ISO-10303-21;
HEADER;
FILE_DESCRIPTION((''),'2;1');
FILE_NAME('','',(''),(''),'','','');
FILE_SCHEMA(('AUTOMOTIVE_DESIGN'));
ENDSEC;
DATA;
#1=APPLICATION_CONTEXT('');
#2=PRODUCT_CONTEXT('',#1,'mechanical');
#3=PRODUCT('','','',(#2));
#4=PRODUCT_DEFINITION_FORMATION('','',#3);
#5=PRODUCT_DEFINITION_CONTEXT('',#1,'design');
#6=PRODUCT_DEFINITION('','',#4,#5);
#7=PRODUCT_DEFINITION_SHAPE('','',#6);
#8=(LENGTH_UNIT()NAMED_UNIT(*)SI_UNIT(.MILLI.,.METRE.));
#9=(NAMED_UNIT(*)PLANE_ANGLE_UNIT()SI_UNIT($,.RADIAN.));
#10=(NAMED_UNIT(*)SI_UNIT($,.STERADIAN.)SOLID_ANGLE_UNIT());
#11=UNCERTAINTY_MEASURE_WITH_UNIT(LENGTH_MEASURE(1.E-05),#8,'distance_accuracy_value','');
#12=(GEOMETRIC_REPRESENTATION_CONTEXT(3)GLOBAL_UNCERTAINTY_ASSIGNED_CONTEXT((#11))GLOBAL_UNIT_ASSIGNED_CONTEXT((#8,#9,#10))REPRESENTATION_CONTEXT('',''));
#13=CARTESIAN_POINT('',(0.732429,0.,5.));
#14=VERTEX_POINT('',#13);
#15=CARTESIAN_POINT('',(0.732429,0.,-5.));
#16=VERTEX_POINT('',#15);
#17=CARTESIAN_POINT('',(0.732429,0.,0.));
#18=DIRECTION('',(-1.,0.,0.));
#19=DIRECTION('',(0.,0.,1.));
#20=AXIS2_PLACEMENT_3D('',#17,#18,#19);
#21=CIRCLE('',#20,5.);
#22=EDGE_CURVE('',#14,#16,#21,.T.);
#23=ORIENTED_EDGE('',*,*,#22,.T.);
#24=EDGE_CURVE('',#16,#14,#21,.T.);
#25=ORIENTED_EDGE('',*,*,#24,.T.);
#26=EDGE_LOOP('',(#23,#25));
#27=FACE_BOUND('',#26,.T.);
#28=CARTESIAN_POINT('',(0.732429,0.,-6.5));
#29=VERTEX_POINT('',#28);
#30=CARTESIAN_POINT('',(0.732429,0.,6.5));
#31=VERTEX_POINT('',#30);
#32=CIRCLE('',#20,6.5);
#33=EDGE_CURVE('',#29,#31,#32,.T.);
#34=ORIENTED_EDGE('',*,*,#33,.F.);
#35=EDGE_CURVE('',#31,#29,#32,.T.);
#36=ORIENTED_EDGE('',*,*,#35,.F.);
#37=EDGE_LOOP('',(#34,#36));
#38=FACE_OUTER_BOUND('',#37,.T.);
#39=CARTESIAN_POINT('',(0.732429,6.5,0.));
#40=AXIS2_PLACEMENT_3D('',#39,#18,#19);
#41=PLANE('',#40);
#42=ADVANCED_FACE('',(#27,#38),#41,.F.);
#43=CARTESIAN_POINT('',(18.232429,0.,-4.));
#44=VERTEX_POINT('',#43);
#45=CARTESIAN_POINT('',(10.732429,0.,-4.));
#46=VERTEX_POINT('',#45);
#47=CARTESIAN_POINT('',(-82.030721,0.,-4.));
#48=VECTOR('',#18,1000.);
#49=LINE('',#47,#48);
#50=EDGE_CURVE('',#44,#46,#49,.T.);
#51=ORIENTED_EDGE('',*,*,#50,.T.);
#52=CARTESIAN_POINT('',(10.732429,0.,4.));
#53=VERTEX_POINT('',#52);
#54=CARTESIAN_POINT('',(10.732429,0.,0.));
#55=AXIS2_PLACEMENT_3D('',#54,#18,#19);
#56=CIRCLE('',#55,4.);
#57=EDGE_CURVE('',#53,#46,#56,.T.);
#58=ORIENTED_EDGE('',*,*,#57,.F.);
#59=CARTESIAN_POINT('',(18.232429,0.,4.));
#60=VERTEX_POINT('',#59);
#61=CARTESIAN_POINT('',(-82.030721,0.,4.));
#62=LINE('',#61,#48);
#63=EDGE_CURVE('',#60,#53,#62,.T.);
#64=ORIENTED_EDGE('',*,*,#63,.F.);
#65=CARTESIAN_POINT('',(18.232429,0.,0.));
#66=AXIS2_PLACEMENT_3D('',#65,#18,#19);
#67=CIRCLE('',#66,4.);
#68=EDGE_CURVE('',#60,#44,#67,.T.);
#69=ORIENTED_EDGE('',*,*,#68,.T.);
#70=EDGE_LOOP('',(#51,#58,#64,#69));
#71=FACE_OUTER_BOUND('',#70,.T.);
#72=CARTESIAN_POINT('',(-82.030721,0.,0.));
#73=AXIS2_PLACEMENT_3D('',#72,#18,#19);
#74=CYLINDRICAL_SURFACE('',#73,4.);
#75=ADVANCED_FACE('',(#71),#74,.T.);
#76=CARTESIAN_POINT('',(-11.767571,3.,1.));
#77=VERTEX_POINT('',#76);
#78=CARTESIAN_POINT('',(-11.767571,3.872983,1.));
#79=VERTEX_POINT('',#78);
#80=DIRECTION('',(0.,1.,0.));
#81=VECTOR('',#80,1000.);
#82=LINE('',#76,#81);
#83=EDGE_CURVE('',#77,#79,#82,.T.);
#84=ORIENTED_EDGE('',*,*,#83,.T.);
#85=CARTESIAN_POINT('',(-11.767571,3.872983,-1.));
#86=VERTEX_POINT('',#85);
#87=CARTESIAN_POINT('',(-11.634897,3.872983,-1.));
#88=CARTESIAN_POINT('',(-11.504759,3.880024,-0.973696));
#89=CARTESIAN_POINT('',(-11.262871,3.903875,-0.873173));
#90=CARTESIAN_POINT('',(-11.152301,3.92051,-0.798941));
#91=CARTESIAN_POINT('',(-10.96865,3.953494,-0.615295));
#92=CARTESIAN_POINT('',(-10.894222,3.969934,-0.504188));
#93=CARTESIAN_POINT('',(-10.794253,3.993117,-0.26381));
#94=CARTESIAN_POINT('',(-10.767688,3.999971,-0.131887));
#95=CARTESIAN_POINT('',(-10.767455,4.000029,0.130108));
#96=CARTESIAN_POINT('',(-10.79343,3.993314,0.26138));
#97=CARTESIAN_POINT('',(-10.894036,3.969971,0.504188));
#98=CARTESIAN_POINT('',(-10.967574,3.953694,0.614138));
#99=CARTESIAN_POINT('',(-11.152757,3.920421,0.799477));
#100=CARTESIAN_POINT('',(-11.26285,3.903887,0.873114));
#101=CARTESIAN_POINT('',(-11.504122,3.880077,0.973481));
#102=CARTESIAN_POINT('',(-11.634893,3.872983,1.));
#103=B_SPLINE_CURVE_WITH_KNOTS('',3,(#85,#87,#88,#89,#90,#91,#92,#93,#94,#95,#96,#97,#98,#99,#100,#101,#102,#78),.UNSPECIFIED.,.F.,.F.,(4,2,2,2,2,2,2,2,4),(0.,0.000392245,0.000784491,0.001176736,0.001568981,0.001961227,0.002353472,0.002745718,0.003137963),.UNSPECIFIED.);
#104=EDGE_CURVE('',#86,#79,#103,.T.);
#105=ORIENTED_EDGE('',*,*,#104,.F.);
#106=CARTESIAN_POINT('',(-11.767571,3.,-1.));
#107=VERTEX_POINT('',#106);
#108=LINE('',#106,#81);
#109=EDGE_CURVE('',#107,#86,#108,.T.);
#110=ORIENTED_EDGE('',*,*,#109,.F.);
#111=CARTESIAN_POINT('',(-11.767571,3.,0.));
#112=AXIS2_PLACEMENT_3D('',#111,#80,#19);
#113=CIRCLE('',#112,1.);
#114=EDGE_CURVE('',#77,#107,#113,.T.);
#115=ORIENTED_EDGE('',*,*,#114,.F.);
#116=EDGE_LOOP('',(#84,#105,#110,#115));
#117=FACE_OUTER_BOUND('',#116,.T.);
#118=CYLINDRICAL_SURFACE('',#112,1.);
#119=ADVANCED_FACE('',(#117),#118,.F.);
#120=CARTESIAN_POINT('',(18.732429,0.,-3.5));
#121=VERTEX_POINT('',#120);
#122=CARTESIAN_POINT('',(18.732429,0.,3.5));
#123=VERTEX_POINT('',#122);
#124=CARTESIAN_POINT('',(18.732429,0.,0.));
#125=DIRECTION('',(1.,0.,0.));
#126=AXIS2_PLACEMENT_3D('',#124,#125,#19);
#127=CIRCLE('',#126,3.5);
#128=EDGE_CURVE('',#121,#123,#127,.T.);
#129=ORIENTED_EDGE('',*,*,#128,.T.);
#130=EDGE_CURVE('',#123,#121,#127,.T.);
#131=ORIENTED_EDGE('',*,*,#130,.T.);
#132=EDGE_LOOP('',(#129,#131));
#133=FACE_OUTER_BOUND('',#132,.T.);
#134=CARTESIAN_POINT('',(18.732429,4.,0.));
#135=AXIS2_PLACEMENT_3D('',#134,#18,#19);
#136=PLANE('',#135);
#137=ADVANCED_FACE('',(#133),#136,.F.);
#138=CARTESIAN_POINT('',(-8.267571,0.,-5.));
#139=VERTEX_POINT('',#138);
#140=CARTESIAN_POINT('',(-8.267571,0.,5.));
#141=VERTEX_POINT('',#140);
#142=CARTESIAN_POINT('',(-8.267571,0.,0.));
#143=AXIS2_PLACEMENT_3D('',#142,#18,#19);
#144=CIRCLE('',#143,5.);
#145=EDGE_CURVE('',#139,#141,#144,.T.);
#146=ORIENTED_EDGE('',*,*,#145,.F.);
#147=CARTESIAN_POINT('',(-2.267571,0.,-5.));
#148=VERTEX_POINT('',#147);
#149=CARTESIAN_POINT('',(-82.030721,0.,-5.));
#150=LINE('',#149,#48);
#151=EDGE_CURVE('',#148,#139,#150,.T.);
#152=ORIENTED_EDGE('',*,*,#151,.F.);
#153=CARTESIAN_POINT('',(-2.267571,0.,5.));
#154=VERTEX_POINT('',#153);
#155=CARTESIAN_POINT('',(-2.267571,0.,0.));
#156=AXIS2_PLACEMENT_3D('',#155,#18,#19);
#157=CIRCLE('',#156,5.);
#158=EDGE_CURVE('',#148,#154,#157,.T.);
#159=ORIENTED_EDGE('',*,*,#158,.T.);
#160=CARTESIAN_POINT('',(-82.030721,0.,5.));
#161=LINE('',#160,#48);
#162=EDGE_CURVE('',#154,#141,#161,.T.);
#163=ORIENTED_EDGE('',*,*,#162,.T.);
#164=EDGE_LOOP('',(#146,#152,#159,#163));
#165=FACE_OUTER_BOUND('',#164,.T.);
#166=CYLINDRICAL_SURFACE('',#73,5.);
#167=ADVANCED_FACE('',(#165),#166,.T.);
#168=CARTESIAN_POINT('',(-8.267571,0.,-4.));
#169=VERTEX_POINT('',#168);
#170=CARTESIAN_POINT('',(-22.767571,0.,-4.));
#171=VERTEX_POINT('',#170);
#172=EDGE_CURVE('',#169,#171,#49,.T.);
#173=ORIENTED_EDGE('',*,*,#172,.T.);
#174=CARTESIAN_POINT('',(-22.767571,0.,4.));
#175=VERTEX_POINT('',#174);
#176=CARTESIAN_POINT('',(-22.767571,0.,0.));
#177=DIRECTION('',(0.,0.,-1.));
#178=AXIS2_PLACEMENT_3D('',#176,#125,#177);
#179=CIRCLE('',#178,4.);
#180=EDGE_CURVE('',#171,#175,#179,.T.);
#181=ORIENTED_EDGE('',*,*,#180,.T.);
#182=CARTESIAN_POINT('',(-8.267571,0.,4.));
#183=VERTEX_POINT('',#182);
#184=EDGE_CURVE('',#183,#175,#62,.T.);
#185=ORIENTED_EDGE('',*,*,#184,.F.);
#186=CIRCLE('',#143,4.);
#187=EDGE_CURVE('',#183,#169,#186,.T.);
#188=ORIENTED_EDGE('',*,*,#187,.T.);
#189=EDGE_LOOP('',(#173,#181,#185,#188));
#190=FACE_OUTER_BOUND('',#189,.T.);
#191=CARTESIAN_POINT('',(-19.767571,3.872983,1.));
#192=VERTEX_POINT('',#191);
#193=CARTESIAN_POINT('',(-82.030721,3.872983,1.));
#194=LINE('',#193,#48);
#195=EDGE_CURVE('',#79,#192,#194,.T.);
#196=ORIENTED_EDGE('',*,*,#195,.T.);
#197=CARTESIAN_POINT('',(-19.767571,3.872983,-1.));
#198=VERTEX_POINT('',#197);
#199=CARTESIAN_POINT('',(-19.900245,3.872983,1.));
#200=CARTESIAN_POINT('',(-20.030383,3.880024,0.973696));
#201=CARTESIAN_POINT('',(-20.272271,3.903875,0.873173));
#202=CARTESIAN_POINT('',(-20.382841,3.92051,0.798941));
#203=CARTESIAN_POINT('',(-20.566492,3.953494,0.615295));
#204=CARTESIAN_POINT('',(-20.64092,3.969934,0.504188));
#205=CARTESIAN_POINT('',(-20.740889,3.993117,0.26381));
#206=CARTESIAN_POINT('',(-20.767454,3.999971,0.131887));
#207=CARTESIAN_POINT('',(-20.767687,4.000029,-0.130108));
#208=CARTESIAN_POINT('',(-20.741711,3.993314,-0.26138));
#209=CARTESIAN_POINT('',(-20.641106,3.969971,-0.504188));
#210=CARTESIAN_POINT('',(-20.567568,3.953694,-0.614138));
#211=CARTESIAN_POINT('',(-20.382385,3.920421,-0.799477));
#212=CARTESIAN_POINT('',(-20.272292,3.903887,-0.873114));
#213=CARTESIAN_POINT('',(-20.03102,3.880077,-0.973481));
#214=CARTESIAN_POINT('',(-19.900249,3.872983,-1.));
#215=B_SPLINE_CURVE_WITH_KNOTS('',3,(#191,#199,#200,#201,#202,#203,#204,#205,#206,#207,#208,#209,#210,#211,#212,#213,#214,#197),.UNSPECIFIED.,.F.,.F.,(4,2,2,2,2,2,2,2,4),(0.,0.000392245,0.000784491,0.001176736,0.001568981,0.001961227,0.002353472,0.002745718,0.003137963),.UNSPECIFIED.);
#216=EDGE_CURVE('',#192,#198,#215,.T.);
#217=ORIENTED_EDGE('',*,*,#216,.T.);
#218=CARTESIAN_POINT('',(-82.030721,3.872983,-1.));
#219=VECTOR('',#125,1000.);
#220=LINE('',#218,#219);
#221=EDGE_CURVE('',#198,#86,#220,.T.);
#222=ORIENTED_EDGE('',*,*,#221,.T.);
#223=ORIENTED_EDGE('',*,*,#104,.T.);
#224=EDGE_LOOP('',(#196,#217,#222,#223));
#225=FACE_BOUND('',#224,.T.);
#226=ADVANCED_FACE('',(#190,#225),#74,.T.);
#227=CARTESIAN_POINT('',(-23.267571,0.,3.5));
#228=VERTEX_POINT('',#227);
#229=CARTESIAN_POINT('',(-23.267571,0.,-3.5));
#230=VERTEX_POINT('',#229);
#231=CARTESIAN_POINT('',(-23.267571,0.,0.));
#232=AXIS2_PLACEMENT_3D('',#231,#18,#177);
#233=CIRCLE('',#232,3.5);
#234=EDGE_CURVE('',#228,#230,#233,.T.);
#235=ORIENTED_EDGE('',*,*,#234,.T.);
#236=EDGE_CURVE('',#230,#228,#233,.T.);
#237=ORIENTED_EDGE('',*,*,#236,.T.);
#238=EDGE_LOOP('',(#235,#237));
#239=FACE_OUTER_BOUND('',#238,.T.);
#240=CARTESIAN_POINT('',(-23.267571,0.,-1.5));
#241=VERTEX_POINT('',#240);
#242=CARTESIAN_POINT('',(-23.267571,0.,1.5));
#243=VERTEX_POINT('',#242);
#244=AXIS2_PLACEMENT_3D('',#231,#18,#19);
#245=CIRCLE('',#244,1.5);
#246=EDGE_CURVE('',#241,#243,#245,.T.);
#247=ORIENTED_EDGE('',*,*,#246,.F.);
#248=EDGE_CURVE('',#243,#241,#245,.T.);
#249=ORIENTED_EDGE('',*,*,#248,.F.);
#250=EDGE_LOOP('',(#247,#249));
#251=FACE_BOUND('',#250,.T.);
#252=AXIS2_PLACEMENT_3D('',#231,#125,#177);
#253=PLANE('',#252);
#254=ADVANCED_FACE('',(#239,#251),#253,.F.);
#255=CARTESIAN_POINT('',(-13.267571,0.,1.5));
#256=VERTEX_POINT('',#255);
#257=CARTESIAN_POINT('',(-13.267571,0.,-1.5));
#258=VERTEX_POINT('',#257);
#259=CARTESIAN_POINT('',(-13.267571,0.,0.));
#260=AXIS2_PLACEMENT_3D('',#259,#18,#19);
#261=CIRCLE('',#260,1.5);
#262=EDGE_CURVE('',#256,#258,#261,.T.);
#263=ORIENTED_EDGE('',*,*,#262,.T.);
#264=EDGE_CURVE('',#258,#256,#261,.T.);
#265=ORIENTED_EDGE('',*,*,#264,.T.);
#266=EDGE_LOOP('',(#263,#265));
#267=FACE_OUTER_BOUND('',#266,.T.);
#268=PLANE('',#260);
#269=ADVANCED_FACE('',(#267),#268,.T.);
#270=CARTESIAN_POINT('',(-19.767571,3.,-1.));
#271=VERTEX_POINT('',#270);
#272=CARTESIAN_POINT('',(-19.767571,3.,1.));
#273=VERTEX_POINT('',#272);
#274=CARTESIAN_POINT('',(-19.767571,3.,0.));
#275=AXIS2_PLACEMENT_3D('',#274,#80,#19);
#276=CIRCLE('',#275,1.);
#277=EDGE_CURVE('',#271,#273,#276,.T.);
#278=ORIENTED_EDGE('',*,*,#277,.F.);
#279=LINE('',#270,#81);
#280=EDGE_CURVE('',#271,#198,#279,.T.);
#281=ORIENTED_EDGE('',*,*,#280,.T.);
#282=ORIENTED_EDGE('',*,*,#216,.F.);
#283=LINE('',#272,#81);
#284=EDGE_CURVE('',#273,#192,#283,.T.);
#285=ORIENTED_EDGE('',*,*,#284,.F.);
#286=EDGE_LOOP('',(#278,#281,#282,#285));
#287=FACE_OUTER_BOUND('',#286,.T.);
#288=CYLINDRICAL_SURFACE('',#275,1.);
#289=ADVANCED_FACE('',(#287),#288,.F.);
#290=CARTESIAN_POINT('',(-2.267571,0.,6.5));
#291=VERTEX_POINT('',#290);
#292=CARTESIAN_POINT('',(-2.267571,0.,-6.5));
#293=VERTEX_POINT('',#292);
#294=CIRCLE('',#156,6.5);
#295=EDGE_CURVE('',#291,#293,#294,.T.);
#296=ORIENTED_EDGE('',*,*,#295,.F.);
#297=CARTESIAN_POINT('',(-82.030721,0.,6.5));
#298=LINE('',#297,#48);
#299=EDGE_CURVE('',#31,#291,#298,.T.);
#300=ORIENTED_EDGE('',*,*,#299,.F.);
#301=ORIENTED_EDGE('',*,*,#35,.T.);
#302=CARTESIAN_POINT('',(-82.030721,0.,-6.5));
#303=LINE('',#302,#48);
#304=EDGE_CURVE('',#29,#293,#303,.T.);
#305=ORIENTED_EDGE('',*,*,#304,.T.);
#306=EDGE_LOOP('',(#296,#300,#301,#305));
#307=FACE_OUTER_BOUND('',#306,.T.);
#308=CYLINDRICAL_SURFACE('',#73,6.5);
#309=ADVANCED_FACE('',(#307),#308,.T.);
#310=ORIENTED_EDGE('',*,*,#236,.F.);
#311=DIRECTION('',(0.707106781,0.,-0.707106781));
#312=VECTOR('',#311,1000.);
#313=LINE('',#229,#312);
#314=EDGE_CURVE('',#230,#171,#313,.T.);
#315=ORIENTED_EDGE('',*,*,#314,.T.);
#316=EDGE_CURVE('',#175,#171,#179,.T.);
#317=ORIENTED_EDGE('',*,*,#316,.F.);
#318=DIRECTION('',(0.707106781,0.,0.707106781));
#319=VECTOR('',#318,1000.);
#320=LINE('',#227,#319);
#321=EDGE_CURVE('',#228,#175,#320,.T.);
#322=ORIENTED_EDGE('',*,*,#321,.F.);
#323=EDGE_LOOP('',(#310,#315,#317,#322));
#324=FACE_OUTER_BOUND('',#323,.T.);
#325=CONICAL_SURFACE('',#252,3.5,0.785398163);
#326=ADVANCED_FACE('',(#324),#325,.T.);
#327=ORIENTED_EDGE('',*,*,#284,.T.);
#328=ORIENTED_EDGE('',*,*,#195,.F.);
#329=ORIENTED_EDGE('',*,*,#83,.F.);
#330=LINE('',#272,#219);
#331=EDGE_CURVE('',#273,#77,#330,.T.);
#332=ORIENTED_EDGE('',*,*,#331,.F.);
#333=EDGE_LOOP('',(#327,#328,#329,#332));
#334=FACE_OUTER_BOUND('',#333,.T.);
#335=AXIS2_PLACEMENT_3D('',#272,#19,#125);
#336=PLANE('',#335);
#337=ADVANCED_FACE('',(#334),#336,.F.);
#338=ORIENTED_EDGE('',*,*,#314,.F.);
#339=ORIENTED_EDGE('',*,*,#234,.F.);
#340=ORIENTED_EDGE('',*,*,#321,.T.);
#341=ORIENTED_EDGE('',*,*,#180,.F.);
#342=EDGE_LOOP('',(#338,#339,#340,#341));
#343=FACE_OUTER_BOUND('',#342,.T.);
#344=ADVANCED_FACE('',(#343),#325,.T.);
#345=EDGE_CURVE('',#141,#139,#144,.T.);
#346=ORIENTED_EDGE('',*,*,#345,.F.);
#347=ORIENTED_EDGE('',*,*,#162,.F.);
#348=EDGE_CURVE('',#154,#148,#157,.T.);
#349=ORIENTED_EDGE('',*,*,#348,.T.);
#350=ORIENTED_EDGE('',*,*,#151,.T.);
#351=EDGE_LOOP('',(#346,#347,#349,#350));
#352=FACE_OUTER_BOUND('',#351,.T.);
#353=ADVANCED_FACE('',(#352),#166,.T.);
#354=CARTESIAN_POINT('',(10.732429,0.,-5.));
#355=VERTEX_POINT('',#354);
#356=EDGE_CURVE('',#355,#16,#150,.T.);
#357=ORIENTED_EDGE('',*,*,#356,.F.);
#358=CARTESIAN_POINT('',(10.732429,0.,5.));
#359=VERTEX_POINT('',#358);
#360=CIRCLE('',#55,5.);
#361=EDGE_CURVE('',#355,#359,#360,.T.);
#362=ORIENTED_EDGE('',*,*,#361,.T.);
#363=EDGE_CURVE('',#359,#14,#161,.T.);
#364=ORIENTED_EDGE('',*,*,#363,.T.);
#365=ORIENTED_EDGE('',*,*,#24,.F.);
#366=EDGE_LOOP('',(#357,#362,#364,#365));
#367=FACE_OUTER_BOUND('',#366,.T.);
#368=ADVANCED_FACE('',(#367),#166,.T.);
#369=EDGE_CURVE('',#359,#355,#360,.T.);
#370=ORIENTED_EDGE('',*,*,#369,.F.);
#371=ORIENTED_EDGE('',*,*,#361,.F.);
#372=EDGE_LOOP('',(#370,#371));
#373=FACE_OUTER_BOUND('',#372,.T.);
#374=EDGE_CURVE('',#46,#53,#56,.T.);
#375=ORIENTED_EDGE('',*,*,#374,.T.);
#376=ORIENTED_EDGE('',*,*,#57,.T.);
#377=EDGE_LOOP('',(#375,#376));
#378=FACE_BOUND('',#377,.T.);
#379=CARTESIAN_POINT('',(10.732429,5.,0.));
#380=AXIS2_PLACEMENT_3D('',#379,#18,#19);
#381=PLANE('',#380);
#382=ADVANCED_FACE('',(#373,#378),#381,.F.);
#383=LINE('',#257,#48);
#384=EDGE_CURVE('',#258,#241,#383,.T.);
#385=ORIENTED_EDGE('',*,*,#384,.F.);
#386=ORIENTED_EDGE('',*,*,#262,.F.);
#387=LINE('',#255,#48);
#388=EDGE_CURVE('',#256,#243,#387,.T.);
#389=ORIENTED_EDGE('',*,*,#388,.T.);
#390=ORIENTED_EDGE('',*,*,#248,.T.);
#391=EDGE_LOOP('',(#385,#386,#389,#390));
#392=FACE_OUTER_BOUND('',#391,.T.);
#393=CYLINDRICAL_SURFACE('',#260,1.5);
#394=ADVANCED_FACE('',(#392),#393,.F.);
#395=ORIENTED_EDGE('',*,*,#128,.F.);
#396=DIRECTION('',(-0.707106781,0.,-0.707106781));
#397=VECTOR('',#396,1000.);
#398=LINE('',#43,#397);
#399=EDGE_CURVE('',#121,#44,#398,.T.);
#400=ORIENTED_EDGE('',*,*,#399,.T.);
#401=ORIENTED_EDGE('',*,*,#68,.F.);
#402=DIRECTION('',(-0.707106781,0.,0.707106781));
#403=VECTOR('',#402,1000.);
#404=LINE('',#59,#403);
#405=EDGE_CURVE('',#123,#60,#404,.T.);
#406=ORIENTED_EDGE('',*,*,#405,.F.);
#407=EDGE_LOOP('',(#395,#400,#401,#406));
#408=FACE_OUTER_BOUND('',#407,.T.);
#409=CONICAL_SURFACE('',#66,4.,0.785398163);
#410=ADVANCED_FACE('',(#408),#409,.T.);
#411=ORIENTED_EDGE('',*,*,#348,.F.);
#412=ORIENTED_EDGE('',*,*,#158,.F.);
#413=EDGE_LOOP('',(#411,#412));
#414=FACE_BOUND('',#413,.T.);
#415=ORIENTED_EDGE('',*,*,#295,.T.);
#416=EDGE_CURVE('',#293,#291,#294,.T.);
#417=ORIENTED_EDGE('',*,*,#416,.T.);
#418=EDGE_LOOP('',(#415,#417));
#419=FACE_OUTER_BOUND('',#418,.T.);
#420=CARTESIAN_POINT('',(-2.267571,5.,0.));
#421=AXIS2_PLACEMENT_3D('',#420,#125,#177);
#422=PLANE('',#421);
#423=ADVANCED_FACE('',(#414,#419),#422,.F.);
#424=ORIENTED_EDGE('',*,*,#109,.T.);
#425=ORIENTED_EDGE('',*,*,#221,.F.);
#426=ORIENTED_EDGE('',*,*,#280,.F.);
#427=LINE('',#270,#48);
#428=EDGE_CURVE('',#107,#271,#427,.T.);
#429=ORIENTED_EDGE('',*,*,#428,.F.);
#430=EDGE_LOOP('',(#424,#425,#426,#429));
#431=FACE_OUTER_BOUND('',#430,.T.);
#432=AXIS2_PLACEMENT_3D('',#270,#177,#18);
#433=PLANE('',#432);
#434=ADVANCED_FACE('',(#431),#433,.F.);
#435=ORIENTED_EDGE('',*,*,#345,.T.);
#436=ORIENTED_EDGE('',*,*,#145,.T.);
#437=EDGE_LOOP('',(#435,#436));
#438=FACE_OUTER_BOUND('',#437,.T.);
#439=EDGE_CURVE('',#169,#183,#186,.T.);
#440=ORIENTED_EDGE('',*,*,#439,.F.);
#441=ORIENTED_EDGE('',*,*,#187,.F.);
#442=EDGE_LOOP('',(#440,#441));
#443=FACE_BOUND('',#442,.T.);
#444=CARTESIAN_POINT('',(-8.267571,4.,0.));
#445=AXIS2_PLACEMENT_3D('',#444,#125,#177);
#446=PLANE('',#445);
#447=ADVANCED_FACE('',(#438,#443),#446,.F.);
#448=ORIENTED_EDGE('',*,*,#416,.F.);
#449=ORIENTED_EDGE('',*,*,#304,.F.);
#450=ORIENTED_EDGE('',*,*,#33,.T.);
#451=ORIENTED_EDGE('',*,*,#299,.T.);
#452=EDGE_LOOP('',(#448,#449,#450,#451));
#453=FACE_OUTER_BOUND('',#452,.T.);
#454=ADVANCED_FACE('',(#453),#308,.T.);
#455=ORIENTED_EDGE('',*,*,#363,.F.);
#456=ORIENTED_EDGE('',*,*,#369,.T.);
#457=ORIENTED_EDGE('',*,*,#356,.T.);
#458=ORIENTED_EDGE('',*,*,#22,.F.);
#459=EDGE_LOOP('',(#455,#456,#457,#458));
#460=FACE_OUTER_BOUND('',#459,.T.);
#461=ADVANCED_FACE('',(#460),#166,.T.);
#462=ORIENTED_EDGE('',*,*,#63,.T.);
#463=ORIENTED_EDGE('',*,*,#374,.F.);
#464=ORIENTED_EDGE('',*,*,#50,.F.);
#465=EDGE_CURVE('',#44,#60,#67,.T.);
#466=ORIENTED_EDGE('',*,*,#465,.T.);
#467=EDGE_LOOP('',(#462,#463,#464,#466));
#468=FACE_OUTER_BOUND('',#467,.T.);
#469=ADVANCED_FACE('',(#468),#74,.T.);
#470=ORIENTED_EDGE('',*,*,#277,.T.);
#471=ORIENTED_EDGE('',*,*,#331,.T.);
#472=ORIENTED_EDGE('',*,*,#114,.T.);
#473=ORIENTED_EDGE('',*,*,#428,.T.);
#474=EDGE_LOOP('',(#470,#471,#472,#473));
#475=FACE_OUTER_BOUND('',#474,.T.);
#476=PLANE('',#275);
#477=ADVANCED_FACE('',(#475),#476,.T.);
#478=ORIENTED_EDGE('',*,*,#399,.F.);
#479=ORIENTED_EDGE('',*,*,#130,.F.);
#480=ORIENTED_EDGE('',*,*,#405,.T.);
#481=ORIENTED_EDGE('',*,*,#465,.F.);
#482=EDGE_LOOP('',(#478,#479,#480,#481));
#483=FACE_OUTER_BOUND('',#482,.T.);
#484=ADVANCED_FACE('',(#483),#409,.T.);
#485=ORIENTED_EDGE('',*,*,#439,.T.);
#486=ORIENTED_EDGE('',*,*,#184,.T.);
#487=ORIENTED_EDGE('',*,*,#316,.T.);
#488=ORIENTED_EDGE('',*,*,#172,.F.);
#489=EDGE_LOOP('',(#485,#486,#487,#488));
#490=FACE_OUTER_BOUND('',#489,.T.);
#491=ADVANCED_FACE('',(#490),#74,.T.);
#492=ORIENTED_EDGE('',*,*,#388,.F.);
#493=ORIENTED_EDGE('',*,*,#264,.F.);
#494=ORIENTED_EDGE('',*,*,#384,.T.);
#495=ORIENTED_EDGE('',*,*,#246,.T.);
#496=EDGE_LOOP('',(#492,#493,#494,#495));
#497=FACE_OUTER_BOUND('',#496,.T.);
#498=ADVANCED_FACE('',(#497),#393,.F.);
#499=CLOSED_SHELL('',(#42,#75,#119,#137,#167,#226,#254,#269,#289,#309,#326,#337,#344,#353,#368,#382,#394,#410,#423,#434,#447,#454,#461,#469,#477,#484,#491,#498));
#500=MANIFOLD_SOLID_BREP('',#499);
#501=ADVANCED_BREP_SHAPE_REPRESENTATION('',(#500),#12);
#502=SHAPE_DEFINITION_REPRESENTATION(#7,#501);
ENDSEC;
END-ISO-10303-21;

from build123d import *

# Parameters (mm, degrees)
CUT_EXTRUDE_3_DEPTH = 1
SKETCH_5_R          = 1.5
CUT_EXTRUDE_4_DEPTH = 10
CHAMFER_1_SIZE      = 0.5
CHAMFER_2_SIZE      = 0.5


with BuildPart() as part:
    # 草图1 → 旋转2 (revolve)
    with BuildSketch(Plane.XY, mode=Mode.PRIVATE) as revolve_2_sk:
        Polygon((-23.267570956, 0), (-23.267570956, 4), (-8.267570956, 4), (-8.267570956, 5), (-2.267570956, 5), (-2.267570956, 6.5), (0.732429044, 6.5), (0.732429044, 5), (10.732429044, 5), (10.732429044, 4), (18.732429044, 4), (18.732429044, 0), align=None)
    revolve(revolve_2_sk.sketch.rotate(Axis((-82.03072058, 0, 0), (1, 0, 0)), 90), axis=Axis((-82.03072058, 0, 0), (1, 0, 0)))

    # 草图4 → 切除-拉伸3 (cut)
    with BuildSketch(Plane(origin=(0, 4, 0), x_dir=(1, 0, 0), z_dir=(0, 1, 0))):
        with BuildLine():
            Line((-19.767570956, 1), (-11.767570956, 1))
            ThreePointArc((-11.767570956, 1), (-10.767570956, 0), (-11.767570956, -1))
            Line((-11.767570956, -1), (-19.767570956, -1))
            ThreePointArc((-19.767570956, -1), (-20.767570956, 0), (-19.767570956, 1))
        make_face()
    extrude(amount=-CUT_EXTRUDE_3_DEPTH, mode=Mode.SUBTRACT)

    # 草图5 → 切除-拉伸4 (cut)
    with BuildSketch(Plane.ZY.offset(23.267570956)):
        Circle(SKETCH_5_R)
    extrude(amount=-CUT_EXTRUDE_4_DEPTH, mode=Mode.SUBTRACT)

    # 倒角1
    chamfer_1_edges = [part.edges().sort_by_distance(p)[0] for p in [
        (-23.267570956, 0, -4),
    ]]
    chamfer(chamfer_1_edges, length=CHAMFER_1_SIZE)

    # 倒角2
    chamfer_2_edges = [part.edges().sort_by_distance(p)[0] for p in [
        (18.732429044, 0, -4),
    ]]
    chamfer(chamfer_2_edges, length=CHAMFER_2_SIZE)


solid = part.part
